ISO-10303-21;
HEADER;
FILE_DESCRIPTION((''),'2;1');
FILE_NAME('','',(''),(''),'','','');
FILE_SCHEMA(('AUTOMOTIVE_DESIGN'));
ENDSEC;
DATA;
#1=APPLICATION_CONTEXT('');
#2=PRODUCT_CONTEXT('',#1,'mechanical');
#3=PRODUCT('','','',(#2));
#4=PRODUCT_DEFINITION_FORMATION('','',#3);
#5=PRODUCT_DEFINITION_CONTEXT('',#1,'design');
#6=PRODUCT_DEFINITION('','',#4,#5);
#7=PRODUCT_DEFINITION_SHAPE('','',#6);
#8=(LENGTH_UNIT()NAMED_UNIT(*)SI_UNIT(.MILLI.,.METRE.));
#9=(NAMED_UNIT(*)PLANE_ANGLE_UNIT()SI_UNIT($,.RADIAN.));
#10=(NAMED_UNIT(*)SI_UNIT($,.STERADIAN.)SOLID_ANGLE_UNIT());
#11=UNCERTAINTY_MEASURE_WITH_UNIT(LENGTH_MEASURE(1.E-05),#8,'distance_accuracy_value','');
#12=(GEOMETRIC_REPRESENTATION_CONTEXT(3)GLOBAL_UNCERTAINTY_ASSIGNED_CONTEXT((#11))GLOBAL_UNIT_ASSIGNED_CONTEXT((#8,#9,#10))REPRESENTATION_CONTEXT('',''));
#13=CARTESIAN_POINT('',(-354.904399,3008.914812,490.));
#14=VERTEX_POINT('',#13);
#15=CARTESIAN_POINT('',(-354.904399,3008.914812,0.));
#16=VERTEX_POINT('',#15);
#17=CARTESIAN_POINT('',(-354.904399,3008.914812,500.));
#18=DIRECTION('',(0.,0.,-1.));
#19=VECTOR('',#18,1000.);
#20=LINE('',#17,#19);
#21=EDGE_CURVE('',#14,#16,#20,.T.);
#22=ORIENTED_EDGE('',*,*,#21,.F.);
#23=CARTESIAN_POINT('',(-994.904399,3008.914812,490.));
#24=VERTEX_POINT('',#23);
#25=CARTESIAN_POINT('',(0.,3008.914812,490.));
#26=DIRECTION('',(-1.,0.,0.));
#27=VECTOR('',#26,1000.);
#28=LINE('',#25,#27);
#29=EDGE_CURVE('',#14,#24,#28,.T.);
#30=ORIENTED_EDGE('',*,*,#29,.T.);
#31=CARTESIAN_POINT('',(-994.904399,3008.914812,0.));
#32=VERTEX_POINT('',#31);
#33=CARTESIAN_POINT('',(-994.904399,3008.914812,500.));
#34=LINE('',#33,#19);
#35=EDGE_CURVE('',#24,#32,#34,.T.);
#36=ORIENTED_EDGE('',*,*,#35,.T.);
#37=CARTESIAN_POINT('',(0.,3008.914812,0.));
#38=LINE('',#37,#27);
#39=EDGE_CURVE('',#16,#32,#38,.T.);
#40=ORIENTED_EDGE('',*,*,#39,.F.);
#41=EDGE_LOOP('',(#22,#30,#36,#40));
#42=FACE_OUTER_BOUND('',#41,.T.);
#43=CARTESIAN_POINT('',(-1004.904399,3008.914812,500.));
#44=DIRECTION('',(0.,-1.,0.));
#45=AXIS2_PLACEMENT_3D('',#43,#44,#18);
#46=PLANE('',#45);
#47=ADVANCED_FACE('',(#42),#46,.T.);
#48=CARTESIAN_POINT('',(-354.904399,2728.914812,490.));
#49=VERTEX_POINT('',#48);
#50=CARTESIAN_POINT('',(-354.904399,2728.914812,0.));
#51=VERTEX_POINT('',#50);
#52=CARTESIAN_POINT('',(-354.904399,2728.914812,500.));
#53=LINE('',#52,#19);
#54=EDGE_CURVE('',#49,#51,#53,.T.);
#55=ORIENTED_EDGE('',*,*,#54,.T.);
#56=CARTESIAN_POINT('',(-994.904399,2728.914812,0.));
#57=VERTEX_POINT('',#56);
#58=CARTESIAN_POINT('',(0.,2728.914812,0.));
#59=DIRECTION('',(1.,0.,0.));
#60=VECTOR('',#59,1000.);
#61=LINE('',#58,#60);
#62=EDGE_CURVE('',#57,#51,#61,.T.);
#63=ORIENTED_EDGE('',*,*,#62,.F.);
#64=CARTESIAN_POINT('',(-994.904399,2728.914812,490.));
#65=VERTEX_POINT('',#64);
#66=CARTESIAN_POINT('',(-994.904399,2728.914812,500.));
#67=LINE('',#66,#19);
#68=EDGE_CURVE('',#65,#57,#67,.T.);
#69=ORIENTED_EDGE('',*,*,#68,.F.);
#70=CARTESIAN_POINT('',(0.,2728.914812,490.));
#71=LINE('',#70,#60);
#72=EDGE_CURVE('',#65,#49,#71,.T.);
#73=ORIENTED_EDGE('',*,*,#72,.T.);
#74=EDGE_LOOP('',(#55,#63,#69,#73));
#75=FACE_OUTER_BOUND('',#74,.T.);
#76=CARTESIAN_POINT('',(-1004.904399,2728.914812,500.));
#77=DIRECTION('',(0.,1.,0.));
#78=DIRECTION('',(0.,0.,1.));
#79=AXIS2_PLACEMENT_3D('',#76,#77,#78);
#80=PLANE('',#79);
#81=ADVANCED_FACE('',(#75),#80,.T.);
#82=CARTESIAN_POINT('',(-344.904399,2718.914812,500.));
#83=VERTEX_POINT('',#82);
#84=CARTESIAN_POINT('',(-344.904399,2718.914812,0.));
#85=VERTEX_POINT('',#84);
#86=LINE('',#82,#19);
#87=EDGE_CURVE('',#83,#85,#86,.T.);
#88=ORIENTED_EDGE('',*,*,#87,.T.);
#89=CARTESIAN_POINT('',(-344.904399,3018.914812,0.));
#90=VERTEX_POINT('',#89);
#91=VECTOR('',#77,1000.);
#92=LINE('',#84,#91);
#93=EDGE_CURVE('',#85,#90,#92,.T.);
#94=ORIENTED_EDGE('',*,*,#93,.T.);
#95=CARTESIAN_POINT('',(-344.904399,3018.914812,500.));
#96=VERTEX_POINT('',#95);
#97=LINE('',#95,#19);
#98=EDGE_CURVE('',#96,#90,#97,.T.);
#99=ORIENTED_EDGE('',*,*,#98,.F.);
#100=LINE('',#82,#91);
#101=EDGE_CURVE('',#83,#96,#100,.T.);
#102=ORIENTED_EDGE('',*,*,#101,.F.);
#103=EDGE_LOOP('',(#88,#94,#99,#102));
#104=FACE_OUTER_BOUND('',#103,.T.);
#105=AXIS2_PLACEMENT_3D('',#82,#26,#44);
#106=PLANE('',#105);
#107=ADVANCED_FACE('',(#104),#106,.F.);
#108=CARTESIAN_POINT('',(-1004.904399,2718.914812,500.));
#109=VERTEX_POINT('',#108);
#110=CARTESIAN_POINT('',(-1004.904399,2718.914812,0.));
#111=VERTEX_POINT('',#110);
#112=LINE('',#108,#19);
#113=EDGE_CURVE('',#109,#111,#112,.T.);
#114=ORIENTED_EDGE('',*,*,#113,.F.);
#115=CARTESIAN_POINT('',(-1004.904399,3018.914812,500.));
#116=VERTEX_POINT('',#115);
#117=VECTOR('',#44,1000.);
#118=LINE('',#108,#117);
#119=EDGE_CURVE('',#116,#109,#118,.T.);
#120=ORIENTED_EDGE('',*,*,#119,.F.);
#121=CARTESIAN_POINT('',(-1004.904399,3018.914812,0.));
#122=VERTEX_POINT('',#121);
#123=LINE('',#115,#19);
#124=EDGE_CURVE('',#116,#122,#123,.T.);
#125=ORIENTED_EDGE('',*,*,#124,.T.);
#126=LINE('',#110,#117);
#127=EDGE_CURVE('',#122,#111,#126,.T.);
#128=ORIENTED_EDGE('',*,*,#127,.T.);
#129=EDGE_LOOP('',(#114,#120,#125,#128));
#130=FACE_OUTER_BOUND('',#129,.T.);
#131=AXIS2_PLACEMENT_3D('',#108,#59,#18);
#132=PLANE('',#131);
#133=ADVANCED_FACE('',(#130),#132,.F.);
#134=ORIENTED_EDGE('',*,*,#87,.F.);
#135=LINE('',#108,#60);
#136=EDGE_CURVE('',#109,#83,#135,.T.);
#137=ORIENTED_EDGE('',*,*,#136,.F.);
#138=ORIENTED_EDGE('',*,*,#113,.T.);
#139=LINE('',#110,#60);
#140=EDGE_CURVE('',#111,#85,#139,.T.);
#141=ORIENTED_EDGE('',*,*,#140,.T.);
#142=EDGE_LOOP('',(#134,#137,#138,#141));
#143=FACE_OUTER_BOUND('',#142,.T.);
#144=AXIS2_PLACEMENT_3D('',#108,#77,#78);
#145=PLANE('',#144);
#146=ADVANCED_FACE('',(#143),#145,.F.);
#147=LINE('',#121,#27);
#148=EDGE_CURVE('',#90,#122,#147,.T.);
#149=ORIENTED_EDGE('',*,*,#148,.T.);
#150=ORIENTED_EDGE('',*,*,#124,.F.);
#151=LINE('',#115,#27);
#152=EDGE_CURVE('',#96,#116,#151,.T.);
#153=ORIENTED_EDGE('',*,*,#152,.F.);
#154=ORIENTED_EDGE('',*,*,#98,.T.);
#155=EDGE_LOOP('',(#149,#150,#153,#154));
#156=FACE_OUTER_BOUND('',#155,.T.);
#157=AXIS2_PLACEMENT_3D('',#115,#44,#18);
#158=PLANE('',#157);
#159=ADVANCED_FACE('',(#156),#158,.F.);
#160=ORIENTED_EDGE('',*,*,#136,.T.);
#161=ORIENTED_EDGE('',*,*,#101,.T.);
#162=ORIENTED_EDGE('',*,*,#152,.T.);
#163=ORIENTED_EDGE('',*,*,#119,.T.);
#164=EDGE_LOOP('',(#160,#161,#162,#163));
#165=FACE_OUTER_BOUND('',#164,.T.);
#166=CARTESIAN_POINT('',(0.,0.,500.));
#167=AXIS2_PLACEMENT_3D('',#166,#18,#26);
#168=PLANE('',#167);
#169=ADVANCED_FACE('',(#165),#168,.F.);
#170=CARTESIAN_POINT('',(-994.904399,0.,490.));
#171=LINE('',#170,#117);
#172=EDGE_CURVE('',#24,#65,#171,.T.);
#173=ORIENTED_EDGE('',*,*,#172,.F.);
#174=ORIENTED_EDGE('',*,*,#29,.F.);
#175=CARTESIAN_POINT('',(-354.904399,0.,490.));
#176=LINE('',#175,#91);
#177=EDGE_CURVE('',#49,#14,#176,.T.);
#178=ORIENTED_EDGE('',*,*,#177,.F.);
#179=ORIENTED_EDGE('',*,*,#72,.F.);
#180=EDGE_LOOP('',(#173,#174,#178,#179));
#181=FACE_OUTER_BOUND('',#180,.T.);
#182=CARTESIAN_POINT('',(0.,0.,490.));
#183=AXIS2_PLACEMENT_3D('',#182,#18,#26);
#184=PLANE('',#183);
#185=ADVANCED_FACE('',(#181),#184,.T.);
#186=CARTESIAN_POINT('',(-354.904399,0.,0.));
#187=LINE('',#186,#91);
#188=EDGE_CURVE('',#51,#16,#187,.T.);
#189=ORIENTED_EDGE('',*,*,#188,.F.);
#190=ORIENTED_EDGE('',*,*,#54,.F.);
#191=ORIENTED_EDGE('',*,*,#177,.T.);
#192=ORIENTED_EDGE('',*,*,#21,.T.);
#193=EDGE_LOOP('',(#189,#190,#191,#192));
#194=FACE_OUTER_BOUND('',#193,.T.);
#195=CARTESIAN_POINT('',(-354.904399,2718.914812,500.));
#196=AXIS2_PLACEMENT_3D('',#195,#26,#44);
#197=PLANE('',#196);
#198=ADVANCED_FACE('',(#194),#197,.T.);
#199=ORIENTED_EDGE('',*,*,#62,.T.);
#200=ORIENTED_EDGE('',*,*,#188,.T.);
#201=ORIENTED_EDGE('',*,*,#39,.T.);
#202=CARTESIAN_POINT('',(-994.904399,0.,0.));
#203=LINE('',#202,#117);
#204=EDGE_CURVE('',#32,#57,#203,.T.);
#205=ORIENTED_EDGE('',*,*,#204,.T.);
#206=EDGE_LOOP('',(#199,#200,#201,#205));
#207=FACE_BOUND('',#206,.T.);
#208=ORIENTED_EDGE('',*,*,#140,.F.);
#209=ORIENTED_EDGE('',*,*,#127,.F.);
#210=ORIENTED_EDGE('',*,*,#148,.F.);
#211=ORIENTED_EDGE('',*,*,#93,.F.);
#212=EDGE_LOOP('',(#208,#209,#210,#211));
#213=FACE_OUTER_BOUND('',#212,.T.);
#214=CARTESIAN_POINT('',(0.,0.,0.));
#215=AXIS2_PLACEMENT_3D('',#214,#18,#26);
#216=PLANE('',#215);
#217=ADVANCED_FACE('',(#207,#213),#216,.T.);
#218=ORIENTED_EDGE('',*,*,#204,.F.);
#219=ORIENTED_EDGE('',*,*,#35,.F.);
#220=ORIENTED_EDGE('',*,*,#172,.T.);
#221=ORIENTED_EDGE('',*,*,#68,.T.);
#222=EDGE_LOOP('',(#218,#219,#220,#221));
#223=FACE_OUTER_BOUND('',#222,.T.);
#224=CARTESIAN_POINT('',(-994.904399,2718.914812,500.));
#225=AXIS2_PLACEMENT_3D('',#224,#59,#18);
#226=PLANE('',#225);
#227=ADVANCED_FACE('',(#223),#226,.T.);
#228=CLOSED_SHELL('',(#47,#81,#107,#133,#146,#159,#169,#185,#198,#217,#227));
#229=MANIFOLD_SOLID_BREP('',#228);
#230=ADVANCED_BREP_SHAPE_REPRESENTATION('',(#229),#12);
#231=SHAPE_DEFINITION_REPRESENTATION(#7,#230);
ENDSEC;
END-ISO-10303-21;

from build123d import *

# Parameters (mm, degrees)
SKETCH_1_W      = 660
SKETCH_1_H      = 300
EXTRUDE_1_DEPTH = 500
SHELL_1_T       = -10


with BuildPart() as part:
    # 草图1 → 凸台-拉伸1 (new body)
    with BuildSketch(Plane.XY):
        with Locations((-674.904398529, 2868.914811934)):
            Rectangle(SKETCH_1_W, SKETCH_1_H)
    extrude(amount=EXTRUDE_1_DEPTH)

    # 抽壳1
    shell_1_openings = [part.faces().sort_by_distance(p)[0] for p in [
        (-674.904398529, 2868.914811934, 0),
    ]]
    offset(amount=SHELL_1_T, openings=shell_1_openings, kind=Kind.INTERSECTION)


solid = part.part
